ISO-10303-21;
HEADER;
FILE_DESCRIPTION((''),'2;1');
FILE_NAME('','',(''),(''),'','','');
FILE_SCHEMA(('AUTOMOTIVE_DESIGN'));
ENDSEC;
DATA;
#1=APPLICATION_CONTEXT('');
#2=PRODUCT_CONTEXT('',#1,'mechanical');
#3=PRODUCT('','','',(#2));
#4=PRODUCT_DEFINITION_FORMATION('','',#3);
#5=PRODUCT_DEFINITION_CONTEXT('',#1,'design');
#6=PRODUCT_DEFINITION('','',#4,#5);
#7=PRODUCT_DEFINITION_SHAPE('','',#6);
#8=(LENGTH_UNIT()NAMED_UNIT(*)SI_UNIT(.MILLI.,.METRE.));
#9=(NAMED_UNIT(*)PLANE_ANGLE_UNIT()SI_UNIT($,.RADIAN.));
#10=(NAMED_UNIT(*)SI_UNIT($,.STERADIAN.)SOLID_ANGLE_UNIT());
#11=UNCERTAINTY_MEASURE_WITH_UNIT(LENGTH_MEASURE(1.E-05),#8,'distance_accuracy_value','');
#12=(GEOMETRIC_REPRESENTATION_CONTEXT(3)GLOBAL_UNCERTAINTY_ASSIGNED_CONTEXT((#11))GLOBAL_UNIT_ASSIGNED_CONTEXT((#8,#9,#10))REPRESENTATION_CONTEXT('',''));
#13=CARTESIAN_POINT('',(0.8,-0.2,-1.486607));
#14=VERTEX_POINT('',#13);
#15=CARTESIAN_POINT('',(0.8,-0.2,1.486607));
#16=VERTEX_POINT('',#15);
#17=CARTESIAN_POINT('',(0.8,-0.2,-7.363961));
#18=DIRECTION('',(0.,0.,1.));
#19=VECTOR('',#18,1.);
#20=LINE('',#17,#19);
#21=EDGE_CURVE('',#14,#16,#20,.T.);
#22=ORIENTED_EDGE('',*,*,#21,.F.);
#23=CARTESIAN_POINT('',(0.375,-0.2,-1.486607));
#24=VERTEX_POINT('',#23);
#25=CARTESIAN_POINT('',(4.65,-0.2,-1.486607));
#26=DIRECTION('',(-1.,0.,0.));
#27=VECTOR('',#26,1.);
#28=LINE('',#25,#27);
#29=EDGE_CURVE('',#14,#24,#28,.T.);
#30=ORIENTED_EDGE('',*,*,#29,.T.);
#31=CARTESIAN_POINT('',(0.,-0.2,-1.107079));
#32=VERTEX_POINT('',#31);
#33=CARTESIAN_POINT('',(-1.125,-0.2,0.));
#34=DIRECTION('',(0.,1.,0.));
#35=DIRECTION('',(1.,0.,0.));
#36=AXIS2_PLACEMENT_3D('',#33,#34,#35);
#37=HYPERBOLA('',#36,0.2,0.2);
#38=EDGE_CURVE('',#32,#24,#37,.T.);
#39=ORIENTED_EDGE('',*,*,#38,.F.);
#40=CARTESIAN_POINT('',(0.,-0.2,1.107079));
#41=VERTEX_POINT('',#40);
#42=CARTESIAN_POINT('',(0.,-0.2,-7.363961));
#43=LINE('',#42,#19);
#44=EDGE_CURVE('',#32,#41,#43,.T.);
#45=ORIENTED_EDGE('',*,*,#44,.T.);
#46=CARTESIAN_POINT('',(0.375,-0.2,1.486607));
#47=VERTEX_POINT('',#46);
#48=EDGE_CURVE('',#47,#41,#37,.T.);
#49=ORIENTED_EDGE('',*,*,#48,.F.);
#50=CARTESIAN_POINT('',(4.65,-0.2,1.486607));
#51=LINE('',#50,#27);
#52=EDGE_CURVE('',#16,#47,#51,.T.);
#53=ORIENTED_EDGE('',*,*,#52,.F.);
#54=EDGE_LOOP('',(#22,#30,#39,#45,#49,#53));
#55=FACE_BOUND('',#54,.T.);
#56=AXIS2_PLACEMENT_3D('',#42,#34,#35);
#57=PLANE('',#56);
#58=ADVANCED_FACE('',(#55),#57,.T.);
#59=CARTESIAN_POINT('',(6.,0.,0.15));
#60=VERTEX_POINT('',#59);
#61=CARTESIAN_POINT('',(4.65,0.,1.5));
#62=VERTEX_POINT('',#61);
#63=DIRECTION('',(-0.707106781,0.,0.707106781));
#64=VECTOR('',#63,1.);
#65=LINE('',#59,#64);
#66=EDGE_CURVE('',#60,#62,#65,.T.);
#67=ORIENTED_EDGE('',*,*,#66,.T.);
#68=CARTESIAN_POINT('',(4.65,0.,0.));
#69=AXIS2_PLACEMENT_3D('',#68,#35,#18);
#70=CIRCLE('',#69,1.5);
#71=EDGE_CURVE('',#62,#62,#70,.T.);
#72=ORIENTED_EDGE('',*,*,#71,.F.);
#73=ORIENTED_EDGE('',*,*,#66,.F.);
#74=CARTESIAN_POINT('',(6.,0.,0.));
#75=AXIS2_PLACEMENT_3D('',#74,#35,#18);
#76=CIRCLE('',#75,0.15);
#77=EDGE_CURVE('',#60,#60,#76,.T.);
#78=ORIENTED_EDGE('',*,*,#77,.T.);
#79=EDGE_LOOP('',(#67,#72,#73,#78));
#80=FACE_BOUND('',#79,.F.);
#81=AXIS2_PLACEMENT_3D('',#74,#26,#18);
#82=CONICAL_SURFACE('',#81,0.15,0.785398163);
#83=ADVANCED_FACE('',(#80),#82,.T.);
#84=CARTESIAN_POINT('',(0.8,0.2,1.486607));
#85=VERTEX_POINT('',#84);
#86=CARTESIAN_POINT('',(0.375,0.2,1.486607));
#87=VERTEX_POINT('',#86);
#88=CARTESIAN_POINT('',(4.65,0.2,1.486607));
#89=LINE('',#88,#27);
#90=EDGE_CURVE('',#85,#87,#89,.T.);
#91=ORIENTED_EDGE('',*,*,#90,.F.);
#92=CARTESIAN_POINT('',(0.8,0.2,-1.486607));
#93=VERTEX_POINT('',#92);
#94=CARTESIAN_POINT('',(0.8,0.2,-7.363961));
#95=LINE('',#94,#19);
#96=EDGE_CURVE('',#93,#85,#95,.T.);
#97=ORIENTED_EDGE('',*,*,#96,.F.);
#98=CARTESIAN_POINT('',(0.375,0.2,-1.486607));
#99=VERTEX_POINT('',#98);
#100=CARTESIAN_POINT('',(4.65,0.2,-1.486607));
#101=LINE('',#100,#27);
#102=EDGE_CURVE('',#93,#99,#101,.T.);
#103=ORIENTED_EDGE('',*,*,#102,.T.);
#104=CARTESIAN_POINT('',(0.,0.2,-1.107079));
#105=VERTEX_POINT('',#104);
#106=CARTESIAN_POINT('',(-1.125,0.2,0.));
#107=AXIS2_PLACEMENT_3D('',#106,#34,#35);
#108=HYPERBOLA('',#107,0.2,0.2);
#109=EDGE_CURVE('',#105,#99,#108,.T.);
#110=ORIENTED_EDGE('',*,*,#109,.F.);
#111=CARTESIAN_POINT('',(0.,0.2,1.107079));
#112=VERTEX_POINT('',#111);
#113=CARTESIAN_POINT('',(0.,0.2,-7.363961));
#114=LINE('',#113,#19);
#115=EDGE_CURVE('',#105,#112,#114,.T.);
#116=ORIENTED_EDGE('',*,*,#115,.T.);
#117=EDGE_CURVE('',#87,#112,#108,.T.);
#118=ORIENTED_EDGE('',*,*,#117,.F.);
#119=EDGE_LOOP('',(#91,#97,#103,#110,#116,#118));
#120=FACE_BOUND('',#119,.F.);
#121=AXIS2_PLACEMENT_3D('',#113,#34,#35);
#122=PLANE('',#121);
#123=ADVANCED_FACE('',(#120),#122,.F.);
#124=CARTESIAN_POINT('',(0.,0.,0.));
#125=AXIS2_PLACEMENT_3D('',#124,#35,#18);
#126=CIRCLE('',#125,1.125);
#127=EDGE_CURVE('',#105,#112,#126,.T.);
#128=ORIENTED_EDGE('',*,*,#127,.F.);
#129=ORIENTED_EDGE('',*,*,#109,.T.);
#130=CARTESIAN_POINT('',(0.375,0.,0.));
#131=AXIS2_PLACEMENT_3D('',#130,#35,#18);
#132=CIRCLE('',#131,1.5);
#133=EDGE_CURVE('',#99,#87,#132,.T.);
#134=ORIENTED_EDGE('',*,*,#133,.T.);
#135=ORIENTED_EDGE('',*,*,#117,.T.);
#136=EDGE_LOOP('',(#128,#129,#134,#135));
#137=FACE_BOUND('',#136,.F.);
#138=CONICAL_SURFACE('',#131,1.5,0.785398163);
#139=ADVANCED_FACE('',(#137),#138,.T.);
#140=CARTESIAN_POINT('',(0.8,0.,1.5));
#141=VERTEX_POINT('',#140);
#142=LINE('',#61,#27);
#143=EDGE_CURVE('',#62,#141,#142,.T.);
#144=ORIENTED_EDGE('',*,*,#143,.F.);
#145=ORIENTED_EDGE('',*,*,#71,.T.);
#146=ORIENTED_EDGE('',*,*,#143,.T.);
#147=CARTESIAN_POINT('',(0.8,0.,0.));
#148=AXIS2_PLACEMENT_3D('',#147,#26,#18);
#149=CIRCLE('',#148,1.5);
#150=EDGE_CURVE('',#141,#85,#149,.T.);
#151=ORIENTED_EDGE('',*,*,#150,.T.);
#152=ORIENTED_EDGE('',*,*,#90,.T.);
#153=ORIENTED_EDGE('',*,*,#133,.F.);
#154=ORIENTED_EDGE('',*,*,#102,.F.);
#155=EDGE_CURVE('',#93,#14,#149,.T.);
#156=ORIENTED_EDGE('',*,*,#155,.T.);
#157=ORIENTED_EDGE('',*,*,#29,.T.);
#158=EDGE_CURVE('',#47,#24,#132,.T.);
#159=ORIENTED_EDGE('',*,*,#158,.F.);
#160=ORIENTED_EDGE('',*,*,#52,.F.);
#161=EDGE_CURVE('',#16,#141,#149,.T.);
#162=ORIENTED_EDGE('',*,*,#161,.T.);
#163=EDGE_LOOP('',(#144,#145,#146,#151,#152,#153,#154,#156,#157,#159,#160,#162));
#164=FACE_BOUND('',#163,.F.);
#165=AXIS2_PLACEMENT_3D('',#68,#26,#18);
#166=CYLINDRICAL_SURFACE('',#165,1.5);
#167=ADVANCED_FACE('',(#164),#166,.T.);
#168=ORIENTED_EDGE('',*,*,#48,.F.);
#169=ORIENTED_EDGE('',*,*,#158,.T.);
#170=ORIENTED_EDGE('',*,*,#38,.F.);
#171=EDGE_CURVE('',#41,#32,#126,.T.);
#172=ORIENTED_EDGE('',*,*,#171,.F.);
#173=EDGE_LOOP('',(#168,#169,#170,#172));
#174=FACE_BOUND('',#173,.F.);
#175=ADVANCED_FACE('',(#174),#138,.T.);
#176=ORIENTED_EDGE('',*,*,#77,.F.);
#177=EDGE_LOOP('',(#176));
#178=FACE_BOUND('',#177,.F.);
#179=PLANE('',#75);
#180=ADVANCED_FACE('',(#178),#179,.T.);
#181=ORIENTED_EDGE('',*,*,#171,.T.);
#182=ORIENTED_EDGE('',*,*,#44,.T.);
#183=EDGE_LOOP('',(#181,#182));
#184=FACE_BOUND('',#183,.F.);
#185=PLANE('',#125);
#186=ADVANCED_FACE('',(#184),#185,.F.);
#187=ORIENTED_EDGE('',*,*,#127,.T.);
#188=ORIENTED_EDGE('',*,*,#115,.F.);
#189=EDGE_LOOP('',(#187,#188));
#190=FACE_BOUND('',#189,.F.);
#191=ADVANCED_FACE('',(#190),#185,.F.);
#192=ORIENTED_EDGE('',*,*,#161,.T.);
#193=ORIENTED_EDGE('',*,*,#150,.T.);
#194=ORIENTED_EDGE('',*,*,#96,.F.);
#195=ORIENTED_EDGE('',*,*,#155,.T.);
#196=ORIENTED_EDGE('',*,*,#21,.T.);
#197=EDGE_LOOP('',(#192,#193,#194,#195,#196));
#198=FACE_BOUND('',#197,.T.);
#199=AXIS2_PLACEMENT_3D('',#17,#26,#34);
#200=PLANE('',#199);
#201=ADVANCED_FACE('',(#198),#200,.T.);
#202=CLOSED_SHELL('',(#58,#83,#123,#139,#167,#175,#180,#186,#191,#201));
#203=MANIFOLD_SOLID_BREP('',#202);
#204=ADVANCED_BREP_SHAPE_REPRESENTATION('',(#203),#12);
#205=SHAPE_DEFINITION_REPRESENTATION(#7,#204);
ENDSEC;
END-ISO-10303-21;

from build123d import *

# Parameters (mm, degrees)
NOTCH_DEPTH      = 7.363961031
NOTCH_DEPTH_BACK = 7.363961031
SKETCH2_W        = 0.8
SKETCH2_H        = 0.4


with BuildPart() as part:
    # Sketch1 → Base (revolve)
    with BuildSketch(Plane.XY, mode=Mode.PRIVATE) as base_sk:
        Polygon((0, 0), (6, 0), (6, 0.15), (4.65, 1.5), (0.375, 1.5), (0, 1.125), align=None)
    revolve(base_sk.sketch.rotate(Axis((-14.774129749, 0, 0), (1, 0, 0)), 90), axis=Axis((-14.774129749, 0, 0), (1, 0, 0)))

    # Sketch2 → Notch (cut, two sides: drawn at the far end of the back side and taken through both)
    with BuildSketch(Plane.XY.offset(-NOTCH_DEPTH_BACK)):
        with Locations((0.4, 0)):
            Rectangle(SKETCH2_W, SKETCH2_H)
    extrude(amount=NOTCH_DEPTH + NOTCH_DEPTH_BACK, mode=Mode.SUBTRACT)


solid = part.part
